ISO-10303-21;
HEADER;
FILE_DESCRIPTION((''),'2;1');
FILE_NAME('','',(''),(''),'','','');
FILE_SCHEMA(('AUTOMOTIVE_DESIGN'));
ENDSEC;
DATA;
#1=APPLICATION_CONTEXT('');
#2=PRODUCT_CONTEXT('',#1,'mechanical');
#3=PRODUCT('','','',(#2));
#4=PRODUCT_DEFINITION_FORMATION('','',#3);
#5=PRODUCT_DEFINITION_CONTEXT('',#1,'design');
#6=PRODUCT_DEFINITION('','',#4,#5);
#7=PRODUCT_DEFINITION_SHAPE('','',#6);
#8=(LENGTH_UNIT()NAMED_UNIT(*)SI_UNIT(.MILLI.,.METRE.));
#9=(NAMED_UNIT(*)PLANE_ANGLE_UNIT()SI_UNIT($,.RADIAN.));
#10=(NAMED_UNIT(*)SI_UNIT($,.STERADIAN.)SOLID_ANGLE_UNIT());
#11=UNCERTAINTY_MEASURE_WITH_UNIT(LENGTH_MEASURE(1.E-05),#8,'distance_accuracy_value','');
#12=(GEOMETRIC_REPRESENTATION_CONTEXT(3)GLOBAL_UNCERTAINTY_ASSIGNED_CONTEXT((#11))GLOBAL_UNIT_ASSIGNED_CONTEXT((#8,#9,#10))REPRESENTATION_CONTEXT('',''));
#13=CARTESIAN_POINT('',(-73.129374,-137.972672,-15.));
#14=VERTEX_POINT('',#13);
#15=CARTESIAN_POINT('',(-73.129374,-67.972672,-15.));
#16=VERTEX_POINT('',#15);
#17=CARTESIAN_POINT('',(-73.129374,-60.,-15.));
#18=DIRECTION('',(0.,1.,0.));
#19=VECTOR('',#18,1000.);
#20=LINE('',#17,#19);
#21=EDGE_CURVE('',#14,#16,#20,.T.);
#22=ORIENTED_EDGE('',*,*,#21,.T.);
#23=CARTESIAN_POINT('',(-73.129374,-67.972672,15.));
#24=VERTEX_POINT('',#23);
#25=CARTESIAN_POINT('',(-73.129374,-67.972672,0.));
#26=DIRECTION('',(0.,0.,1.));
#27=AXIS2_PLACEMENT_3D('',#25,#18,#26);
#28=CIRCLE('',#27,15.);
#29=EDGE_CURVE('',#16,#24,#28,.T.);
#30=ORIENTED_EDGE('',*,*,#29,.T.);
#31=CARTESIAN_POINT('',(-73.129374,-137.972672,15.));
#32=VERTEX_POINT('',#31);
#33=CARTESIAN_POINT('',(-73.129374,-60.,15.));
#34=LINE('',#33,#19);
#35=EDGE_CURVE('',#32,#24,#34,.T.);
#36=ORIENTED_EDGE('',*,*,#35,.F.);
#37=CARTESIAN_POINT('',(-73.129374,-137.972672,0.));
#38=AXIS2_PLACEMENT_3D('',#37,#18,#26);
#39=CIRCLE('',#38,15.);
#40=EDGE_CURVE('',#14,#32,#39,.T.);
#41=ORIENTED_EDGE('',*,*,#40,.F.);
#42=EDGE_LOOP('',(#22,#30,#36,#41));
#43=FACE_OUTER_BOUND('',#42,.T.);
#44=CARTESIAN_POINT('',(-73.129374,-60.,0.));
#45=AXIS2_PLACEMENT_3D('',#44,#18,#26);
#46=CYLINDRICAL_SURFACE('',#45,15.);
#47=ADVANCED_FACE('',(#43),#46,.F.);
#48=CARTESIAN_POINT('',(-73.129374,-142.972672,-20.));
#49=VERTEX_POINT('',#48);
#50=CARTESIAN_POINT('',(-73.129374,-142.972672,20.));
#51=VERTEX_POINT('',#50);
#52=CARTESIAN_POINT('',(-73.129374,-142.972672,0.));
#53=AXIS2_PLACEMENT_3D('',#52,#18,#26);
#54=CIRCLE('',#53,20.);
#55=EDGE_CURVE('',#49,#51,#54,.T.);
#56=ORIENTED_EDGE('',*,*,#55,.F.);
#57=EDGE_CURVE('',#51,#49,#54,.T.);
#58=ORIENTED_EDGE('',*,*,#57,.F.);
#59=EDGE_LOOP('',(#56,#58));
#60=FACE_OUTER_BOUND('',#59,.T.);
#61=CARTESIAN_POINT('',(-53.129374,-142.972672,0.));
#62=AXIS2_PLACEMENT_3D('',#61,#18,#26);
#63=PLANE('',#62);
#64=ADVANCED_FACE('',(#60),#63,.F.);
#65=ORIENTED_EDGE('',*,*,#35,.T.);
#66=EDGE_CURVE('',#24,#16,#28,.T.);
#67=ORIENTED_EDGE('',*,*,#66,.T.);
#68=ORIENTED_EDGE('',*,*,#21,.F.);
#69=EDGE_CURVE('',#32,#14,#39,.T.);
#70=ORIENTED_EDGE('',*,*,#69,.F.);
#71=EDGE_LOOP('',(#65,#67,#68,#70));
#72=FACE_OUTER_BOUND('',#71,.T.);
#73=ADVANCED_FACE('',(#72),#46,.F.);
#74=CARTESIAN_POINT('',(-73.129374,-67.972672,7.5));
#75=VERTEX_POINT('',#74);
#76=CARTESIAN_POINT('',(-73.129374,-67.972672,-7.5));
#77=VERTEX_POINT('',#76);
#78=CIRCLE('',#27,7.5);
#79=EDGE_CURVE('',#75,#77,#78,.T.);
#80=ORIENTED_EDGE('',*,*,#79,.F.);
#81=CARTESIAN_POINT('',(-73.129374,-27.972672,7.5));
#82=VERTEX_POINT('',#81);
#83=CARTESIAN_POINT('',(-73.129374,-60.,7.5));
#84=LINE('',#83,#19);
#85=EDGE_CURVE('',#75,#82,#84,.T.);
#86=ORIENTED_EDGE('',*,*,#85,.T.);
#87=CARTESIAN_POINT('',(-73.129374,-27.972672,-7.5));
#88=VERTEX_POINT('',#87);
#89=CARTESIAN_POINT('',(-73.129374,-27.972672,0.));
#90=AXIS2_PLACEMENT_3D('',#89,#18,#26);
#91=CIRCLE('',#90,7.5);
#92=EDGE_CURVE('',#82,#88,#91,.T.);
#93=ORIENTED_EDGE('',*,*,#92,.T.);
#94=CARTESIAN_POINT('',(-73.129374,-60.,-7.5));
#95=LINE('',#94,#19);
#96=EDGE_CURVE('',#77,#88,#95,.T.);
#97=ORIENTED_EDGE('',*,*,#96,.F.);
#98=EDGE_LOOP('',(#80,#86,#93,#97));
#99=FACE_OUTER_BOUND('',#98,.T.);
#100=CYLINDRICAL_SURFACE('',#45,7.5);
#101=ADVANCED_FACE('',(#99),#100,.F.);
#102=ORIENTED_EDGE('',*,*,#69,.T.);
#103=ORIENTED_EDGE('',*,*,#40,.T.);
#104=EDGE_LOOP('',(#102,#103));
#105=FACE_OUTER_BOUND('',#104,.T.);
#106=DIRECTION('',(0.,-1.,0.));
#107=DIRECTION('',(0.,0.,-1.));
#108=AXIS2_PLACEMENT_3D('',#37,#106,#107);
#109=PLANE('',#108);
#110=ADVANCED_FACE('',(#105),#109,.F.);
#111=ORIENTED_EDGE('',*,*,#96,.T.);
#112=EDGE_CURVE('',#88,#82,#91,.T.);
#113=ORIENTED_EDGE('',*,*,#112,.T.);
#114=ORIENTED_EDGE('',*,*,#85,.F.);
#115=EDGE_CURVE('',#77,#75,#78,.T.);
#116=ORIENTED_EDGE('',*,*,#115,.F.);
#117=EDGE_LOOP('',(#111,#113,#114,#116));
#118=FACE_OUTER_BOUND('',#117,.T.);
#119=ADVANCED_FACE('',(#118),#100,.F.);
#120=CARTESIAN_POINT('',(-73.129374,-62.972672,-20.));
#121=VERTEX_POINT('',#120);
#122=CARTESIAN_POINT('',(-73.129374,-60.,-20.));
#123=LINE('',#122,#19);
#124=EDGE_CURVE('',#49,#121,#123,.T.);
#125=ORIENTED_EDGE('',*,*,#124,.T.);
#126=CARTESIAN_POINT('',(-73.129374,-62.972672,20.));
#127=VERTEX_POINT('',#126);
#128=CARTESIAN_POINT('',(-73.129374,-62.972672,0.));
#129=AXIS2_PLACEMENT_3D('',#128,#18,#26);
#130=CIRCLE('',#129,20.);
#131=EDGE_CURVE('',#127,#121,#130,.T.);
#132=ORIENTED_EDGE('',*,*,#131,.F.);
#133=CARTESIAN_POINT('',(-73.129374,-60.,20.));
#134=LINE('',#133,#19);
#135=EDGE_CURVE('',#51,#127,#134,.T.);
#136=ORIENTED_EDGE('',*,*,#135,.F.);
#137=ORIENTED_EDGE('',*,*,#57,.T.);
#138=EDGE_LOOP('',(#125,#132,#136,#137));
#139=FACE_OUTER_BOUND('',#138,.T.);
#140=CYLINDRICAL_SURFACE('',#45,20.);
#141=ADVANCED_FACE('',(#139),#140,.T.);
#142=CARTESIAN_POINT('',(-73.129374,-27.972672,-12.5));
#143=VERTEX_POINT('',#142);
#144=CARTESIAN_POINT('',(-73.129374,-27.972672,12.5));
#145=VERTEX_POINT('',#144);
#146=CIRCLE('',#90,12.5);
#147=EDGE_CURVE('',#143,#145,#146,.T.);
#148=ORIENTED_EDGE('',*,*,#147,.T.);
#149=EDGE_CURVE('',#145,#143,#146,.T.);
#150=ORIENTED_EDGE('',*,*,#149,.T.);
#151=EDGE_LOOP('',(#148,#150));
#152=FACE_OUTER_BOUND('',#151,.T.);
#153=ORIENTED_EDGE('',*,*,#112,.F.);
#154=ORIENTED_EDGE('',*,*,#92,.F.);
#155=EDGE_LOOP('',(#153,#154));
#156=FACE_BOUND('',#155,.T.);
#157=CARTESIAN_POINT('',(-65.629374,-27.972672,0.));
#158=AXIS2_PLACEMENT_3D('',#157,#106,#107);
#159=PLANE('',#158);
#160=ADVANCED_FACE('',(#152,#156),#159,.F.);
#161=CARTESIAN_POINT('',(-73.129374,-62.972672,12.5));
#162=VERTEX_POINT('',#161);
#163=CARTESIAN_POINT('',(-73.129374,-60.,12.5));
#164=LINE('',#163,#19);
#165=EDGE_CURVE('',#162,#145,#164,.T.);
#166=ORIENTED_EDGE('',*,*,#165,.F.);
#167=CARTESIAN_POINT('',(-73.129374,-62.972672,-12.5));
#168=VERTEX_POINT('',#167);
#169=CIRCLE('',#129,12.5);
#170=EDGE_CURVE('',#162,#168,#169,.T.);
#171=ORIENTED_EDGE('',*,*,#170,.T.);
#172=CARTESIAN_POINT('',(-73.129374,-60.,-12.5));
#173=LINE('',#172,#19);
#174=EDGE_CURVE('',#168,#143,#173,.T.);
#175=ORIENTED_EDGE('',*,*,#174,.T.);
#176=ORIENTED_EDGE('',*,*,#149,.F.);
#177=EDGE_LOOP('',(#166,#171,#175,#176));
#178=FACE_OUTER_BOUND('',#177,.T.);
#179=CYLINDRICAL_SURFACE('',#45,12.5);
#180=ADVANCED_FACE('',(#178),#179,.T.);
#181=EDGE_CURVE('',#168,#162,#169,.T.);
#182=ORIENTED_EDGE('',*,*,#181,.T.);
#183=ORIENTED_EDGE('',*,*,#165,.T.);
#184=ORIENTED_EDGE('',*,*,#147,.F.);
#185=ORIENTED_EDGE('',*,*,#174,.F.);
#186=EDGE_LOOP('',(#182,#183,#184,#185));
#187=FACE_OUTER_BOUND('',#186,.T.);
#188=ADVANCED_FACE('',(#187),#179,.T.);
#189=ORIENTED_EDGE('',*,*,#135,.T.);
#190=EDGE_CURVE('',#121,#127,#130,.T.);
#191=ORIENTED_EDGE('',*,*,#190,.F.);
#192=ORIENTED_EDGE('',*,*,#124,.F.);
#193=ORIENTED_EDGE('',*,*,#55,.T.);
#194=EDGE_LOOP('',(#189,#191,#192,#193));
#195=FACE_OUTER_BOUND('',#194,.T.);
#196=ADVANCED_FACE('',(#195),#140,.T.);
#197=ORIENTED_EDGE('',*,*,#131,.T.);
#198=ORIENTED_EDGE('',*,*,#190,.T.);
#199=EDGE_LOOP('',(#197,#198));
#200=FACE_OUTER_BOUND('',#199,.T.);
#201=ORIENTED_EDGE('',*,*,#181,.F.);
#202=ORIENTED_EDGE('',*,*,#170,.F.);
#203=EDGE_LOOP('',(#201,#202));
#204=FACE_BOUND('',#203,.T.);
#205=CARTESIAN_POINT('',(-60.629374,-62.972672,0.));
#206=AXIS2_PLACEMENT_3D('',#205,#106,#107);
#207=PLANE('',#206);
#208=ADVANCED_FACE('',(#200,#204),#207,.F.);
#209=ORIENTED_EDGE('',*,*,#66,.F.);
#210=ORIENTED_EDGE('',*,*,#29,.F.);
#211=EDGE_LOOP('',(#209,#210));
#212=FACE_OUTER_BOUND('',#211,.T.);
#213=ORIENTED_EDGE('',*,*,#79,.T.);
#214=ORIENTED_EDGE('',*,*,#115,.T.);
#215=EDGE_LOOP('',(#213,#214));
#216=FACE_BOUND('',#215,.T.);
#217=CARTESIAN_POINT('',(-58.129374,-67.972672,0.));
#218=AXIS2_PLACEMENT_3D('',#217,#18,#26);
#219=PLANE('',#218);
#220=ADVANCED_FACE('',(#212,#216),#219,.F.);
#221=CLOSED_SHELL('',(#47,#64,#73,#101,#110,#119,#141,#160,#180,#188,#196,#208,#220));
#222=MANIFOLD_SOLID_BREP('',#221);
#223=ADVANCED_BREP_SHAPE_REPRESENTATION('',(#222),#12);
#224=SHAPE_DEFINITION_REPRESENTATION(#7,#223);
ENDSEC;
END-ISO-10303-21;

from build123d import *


with BuildPart() as part:
    # Sketch1 → Revolve1 (revolve)
    with BuildSketch(Plane.XY, mode=Mode.PRIVATE) as revolve1_sk:
        Polygon((-65.629373749, -27.972671928), (-60.629373749, -27.972671928), (-60.629373749, -62.972671928), (-53.129373749, -62.972671928), (-53.129373749, -142.972671928), (-73.129373749, -142.972671928), (-73.129373749, -137.972671928), (-58.129373749, -137.972671928), (-58.129373749, -67.972671928), (-65.629373749, -67.972671928), align=None)
    revolve(revolve1_sk.sketch.rotate(Axis((-73.129373749, -60, 0), (0, -1, 0)), 90), axis=Axis((-73.129373749, -60, 0), (0, -1, 0)))


solid = part.part
